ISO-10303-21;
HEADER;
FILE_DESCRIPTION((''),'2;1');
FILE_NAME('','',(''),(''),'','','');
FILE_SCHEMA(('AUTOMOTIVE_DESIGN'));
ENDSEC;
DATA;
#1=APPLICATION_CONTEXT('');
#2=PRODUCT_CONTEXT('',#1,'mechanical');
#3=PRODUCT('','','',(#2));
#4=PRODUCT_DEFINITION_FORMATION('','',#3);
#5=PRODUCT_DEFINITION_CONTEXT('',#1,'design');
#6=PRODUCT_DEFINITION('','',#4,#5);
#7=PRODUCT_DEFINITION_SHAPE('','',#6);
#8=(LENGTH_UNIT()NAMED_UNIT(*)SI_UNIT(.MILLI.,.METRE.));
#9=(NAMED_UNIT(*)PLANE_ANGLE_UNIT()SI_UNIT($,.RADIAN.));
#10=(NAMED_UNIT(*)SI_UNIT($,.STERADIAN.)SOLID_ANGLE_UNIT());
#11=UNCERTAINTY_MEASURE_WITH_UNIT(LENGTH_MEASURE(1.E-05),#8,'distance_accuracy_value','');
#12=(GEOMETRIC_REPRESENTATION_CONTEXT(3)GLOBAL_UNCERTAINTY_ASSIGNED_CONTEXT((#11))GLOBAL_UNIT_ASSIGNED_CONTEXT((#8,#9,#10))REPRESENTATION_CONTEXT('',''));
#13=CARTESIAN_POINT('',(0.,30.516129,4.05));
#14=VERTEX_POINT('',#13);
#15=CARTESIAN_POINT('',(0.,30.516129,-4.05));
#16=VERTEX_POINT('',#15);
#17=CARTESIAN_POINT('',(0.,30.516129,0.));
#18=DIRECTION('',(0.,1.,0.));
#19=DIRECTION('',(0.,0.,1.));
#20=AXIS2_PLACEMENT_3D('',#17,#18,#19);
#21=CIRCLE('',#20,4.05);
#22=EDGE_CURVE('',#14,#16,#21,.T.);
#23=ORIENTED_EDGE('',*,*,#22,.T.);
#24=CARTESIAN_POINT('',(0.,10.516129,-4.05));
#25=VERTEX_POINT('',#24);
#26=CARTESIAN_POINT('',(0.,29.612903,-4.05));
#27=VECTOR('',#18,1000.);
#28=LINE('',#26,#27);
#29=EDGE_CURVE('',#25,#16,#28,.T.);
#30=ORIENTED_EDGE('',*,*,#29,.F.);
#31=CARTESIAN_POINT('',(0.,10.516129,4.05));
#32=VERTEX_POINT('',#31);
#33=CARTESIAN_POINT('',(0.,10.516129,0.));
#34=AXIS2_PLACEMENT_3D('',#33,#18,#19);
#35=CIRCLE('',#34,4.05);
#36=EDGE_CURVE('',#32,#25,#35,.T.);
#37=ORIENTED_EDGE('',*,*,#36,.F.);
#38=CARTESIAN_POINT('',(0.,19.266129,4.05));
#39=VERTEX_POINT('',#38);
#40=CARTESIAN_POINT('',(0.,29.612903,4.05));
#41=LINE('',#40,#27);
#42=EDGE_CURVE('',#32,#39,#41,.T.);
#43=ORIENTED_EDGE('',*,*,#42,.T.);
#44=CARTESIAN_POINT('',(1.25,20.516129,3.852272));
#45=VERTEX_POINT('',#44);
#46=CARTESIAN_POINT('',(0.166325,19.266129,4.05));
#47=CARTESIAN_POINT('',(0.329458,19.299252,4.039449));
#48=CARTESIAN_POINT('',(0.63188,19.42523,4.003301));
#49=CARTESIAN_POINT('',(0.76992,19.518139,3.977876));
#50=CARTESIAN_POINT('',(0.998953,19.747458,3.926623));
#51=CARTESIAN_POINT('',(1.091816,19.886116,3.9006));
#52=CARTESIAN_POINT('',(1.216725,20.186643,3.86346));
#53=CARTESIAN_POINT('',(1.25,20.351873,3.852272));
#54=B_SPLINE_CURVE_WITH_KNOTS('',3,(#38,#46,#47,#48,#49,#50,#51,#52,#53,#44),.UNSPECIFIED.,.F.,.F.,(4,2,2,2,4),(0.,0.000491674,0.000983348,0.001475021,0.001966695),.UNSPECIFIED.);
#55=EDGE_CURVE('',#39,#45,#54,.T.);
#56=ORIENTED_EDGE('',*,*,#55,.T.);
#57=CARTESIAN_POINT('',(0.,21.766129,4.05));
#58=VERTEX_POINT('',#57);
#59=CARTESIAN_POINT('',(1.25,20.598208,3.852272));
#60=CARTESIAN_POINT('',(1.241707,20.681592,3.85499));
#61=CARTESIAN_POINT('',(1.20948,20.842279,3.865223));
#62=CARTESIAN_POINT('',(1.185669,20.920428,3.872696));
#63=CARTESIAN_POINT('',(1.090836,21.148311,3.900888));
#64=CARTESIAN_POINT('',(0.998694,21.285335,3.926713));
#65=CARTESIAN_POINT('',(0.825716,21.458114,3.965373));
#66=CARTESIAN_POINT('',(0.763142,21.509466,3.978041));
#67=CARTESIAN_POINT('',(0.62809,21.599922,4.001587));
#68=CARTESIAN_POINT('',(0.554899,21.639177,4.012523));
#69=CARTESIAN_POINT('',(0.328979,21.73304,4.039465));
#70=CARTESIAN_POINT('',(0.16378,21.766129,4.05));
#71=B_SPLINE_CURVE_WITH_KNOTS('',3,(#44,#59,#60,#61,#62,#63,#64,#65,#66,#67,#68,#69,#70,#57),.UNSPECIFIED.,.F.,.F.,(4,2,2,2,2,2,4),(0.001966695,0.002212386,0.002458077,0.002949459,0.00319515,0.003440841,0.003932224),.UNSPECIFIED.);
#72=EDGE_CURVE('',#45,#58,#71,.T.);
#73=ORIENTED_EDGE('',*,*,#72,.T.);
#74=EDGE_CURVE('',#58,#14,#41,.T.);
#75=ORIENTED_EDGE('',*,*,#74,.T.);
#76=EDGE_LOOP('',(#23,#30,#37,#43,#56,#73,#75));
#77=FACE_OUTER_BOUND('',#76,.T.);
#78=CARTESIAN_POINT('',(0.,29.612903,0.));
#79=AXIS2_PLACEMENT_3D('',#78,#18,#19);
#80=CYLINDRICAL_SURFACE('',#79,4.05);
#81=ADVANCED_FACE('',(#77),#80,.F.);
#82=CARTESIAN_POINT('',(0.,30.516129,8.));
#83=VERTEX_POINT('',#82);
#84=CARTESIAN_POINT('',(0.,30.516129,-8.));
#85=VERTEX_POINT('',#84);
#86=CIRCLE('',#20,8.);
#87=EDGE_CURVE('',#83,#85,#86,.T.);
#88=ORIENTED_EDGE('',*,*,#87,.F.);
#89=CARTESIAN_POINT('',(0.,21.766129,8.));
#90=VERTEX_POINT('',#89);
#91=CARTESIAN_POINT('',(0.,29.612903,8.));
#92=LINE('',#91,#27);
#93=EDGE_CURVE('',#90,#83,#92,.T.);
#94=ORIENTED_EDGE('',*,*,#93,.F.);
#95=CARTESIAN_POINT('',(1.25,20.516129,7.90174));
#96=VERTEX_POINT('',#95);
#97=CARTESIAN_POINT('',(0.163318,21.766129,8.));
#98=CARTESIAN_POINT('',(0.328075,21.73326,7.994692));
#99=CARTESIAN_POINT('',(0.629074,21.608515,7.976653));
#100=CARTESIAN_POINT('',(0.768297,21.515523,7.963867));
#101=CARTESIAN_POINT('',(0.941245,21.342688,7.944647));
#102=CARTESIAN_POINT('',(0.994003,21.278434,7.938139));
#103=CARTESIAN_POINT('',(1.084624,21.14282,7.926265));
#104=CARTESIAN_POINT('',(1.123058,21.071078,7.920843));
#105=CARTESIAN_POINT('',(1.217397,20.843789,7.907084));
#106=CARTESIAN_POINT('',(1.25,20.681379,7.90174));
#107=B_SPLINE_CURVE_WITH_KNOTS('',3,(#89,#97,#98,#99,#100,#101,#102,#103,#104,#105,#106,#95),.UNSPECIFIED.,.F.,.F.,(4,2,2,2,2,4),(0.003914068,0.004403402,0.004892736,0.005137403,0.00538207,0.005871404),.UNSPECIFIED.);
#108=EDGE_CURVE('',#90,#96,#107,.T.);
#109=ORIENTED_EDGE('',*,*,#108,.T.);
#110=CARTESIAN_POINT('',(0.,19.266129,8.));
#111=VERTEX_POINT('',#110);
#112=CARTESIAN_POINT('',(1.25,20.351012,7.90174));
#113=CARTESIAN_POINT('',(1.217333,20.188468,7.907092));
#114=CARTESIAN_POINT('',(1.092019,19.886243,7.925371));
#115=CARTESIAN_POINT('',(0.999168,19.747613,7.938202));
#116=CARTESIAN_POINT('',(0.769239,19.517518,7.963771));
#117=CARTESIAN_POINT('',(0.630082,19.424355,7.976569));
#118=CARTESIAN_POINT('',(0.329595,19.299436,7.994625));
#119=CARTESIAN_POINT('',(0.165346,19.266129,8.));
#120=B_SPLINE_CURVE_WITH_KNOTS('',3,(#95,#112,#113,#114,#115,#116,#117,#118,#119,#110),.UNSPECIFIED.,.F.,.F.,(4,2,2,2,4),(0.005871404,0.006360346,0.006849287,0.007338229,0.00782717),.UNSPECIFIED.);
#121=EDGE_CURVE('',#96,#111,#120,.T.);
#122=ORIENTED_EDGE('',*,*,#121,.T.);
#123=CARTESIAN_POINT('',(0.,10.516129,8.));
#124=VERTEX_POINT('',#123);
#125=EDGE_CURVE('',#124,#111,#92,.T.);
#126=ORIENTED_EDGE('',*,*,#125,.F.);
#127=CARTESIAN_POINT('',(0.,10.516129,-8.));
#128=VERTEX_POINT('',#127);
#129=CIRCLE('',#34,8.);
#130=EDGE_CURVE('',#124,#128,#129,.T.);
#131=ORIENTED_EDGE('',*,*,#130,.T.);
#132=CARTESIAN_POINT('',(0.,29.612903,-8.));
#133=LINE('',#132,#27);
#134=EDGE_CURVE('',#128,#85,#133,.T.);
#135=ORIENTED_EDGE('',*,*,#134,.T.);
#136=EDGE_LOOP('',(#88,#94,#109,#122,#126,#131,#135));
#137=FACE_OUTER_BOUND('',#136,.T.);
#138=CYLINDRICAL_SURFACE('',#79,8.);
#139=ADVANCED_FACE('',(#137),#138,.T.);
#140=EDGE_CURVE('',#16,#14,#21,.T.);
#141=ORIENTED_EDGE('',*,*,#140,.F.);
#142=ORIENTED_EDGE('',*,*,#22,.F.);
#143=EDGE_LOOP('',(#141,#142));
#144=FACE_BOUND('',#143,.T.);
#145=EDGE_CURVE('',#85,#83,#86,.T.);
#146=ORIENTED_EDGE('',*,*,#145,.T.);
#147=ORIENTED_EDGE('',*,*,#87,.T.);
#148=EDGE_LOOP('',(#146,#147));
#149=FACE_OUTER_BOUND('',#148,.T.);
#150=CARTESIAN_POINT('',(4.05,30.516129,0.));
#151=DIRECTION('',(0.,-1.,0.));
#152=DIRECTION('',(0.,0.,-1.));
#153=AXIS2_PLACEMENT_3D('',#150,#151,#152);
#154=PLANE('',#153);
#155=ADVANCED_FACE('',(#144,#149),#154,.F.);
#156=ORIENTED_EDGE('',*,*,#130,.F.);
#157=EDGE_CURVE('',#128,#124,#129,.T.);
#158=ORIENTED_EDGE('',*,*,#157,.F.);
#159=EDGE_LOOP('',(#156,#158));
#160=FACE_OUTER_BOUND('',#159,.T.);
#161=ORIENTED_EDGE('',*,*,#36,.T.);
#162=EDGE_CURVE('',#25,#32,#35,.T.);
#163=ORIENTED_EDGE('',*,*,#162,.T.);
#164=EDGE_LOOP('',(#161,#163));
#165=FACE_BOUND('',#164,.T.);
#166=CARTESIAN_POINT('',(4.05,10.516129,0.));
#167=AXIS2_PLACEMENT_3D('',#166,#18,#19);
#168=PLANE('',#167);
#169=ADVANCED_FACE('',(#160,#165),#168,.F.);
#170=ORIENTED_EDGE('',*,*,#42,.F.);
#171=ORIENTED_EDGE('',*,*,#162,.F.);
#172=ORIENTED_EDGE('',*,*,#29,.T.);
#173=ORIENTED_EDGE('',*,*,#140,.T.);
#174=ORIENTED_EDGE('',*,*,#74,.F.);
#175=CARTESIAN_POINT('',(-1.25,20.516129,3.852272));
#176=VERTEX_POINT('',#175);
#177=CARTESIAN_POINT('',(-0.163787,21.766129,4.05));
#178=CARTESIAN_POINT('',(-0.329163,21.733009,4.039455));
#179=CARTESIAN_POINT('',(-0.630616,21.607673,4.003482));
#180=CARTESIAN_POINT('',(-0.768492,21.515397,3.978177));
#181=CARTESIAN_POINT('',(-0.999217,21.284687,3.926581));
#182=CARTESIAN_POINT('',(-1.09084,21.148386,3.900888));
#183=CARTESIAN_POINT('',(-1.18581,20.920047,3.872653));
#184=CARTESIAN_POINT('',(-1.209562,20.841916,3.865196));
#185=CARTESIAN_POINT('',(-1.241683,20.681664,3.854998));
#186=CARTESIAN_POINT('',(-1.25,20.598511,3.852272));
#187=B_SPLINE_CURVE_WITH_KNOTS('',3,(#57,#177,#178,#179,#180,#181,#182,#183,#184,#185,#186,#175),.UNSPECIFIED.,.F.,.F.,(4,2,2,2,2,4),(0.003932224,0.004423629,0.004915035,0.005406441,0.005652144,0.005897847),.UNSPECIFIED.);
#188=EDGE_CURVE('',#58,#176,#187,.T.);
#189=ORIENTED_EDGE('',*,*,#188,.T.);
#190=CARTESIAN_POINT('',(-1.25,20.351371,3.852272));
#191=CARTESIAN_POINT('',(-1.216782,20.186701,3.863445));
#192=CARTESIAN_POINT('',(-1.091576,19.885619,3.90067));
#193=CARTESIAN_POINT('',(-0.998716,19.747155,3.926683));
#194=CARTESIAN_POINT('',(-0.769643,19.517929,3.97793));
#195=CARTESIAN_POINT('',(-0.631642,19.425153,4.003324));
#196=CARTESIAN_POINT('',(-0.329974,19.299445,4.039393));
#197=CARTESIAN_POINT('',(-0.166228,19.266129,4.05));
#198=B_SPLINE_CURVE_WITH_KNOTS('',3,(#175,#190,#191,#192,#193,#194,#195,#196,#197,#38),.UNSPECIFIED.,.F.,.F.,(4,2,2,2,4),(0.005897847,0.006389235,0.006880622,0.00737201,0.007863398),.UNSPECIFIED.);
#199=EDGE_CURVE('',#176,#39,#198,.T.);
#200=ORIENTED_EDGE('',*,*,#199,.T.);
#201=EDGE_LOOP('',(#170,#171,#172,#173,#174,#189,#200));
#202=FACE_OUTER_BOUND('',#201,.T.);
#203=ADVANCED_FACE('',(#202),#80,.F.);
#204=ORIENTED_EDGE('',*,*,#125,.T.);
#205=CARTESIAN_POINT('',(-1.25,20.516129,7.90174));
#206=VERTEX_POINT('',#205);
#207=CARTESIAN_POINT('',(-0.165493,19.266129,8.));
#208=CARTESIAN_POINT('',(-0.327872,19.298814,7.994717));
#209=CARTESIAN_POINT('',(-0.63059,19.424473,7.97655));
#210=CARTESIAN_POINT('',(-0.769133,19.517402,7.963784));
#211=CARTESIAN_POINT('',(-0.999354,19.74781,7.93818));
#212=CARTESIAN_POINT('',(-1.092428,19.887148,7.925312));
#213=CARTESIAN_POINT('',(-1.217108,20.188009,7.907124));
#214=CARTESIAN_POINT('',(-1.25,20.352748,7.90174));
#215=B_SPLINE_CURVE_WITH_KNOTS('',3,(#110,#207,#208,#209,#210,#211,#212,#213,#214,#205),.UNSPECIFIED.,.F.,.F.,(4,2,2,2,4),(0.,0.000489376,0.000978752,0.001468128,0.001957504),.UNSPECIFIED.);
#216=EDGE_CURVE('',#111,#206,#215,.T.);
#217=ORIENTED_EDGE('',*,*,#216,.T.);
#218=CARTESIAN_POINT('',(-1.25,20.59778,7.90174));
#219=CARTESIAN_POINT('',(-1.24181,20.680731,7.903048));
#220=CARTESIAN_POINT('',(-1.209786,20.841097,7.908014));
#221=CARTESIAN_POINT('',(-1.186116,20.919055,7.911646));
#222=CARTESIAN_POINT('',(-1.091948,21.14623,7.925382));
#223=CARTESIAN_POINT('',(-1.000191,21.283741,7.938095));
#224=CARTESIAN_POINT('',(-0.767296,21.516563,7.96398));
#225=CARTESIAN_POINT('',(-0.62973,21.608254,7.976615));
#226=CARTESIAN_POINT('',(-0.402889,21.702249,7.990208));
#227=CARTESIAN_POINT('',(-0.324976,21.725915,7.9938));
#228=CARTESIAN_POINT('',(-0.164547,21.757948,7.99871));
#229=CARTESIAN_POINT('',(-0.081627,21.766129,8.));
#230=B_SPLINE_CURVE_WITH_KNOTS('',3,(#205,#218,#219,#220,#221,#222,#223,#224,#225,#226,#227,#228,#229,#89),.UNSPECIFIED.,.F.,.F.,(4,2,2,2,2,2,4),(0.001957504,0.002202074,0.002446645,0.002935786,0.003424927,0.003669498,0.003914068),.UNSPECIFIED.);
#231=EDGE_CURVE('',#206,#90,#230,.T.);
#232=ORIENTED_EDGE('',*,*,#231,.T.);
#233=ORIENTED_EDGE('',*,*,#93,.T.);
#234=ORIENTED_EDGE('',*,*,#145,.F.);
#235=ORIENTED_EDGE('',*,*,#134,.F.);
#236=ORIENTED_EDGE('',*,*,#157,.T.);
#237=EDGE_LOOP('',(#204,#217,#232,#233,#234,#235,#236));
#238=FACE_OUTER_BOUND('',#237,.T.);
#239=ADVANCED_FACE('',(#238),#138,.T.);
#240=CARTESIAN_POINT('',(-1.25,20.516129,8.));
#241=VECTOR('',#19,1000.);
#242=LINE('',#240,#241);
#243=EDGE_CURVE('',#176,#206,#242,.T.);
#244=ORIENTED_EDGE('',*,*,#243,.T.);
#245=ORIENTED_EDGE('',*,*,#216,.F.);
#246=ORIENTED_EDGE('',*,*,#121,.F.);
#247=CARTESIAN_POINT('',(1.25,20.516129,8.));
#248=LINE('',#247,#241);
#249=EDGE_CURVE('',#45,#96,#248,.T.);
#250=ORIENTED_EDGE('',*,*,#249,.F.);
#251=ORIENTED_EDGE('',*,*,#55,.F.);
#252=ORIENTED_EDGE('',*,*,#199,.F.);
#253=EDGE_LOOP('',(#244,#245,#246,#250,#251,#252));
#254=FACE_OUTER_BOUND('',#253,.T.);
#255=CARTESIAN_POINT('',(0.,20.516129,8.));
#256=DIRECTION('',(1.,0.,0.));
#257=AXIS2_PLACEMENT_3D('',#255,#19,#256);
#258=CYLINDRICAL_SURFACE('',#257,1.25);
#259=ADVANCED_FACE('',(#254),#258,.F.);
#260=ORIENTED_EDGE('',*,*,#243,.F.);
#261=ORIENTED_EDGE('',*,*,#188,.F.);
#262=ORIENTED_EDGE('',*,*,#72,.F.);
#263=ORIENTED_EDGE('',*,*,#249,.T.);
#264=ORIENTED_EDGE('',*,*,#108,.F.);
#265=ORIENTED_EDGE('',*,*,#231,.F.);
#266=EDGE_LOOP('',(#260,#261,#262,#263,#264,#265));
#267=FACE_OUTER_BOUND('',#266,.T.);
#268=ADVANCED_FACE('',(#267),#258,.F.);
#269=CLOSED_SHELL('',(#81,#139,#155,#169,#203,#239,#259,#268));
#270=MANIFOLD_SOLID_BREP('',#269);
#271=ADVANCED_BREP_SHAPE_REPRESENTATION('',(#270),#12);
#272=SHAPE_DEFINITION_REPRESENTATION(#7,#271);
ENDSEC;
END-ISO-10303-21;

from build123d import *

# Parameters (mm, degrees)
SKETCH1_W              = 3.95
SKETCH1_H              = 20
M3_TAPPED_HOLE1_REACH  = 22.494
M3_TAPPED_HOLE1_BORE_R = 1.25


with BuildPart() as part:
    # Sketch1 → Revolve1 (revolve)
    with BuildSketch(Plane.XY, mode=Mode.PRIVATE) as revolve1_sk:
        with Locations((6.025, 20.516129032)):
            Rectangle(SKETCH1_W, SKETCH1_H)
    revolve(revolve1_sk.sketch.rotate(Axis((0, 29.612903226, 0), (0, -1, 0)), 90), axis=Axis((0, 29.612903226, 0), (0, -1, 0)))

    # M3 Tapped Hole1 bore (on position points) → M3 Tapped Hole1 (cut, up to next)
    with BuildSketch(Plane(origin=(0, 20.516129032, 8), x_dir=(1, 0, 0), z_dir=(0, 0, 1)), mode=Mode.PRIVATE) as m3_tapped_hole1_sk1:
        Circle(M3_TAPPED_HOLE1_BORE_R)
    m3_tapped_hole1_tool1 = extrude(m3_tapped_hole1_sk1.sketch, amount=-M3_TAPPED_HOLE1_REACH, mode=Mode.PRIVATE) & part.part
    add(m3_tapped_hole1_tool1.solids().sort_by_distance((0, 20.516129, 8))[0], mode=Mode.SUBTRACT)


solid = part.part
